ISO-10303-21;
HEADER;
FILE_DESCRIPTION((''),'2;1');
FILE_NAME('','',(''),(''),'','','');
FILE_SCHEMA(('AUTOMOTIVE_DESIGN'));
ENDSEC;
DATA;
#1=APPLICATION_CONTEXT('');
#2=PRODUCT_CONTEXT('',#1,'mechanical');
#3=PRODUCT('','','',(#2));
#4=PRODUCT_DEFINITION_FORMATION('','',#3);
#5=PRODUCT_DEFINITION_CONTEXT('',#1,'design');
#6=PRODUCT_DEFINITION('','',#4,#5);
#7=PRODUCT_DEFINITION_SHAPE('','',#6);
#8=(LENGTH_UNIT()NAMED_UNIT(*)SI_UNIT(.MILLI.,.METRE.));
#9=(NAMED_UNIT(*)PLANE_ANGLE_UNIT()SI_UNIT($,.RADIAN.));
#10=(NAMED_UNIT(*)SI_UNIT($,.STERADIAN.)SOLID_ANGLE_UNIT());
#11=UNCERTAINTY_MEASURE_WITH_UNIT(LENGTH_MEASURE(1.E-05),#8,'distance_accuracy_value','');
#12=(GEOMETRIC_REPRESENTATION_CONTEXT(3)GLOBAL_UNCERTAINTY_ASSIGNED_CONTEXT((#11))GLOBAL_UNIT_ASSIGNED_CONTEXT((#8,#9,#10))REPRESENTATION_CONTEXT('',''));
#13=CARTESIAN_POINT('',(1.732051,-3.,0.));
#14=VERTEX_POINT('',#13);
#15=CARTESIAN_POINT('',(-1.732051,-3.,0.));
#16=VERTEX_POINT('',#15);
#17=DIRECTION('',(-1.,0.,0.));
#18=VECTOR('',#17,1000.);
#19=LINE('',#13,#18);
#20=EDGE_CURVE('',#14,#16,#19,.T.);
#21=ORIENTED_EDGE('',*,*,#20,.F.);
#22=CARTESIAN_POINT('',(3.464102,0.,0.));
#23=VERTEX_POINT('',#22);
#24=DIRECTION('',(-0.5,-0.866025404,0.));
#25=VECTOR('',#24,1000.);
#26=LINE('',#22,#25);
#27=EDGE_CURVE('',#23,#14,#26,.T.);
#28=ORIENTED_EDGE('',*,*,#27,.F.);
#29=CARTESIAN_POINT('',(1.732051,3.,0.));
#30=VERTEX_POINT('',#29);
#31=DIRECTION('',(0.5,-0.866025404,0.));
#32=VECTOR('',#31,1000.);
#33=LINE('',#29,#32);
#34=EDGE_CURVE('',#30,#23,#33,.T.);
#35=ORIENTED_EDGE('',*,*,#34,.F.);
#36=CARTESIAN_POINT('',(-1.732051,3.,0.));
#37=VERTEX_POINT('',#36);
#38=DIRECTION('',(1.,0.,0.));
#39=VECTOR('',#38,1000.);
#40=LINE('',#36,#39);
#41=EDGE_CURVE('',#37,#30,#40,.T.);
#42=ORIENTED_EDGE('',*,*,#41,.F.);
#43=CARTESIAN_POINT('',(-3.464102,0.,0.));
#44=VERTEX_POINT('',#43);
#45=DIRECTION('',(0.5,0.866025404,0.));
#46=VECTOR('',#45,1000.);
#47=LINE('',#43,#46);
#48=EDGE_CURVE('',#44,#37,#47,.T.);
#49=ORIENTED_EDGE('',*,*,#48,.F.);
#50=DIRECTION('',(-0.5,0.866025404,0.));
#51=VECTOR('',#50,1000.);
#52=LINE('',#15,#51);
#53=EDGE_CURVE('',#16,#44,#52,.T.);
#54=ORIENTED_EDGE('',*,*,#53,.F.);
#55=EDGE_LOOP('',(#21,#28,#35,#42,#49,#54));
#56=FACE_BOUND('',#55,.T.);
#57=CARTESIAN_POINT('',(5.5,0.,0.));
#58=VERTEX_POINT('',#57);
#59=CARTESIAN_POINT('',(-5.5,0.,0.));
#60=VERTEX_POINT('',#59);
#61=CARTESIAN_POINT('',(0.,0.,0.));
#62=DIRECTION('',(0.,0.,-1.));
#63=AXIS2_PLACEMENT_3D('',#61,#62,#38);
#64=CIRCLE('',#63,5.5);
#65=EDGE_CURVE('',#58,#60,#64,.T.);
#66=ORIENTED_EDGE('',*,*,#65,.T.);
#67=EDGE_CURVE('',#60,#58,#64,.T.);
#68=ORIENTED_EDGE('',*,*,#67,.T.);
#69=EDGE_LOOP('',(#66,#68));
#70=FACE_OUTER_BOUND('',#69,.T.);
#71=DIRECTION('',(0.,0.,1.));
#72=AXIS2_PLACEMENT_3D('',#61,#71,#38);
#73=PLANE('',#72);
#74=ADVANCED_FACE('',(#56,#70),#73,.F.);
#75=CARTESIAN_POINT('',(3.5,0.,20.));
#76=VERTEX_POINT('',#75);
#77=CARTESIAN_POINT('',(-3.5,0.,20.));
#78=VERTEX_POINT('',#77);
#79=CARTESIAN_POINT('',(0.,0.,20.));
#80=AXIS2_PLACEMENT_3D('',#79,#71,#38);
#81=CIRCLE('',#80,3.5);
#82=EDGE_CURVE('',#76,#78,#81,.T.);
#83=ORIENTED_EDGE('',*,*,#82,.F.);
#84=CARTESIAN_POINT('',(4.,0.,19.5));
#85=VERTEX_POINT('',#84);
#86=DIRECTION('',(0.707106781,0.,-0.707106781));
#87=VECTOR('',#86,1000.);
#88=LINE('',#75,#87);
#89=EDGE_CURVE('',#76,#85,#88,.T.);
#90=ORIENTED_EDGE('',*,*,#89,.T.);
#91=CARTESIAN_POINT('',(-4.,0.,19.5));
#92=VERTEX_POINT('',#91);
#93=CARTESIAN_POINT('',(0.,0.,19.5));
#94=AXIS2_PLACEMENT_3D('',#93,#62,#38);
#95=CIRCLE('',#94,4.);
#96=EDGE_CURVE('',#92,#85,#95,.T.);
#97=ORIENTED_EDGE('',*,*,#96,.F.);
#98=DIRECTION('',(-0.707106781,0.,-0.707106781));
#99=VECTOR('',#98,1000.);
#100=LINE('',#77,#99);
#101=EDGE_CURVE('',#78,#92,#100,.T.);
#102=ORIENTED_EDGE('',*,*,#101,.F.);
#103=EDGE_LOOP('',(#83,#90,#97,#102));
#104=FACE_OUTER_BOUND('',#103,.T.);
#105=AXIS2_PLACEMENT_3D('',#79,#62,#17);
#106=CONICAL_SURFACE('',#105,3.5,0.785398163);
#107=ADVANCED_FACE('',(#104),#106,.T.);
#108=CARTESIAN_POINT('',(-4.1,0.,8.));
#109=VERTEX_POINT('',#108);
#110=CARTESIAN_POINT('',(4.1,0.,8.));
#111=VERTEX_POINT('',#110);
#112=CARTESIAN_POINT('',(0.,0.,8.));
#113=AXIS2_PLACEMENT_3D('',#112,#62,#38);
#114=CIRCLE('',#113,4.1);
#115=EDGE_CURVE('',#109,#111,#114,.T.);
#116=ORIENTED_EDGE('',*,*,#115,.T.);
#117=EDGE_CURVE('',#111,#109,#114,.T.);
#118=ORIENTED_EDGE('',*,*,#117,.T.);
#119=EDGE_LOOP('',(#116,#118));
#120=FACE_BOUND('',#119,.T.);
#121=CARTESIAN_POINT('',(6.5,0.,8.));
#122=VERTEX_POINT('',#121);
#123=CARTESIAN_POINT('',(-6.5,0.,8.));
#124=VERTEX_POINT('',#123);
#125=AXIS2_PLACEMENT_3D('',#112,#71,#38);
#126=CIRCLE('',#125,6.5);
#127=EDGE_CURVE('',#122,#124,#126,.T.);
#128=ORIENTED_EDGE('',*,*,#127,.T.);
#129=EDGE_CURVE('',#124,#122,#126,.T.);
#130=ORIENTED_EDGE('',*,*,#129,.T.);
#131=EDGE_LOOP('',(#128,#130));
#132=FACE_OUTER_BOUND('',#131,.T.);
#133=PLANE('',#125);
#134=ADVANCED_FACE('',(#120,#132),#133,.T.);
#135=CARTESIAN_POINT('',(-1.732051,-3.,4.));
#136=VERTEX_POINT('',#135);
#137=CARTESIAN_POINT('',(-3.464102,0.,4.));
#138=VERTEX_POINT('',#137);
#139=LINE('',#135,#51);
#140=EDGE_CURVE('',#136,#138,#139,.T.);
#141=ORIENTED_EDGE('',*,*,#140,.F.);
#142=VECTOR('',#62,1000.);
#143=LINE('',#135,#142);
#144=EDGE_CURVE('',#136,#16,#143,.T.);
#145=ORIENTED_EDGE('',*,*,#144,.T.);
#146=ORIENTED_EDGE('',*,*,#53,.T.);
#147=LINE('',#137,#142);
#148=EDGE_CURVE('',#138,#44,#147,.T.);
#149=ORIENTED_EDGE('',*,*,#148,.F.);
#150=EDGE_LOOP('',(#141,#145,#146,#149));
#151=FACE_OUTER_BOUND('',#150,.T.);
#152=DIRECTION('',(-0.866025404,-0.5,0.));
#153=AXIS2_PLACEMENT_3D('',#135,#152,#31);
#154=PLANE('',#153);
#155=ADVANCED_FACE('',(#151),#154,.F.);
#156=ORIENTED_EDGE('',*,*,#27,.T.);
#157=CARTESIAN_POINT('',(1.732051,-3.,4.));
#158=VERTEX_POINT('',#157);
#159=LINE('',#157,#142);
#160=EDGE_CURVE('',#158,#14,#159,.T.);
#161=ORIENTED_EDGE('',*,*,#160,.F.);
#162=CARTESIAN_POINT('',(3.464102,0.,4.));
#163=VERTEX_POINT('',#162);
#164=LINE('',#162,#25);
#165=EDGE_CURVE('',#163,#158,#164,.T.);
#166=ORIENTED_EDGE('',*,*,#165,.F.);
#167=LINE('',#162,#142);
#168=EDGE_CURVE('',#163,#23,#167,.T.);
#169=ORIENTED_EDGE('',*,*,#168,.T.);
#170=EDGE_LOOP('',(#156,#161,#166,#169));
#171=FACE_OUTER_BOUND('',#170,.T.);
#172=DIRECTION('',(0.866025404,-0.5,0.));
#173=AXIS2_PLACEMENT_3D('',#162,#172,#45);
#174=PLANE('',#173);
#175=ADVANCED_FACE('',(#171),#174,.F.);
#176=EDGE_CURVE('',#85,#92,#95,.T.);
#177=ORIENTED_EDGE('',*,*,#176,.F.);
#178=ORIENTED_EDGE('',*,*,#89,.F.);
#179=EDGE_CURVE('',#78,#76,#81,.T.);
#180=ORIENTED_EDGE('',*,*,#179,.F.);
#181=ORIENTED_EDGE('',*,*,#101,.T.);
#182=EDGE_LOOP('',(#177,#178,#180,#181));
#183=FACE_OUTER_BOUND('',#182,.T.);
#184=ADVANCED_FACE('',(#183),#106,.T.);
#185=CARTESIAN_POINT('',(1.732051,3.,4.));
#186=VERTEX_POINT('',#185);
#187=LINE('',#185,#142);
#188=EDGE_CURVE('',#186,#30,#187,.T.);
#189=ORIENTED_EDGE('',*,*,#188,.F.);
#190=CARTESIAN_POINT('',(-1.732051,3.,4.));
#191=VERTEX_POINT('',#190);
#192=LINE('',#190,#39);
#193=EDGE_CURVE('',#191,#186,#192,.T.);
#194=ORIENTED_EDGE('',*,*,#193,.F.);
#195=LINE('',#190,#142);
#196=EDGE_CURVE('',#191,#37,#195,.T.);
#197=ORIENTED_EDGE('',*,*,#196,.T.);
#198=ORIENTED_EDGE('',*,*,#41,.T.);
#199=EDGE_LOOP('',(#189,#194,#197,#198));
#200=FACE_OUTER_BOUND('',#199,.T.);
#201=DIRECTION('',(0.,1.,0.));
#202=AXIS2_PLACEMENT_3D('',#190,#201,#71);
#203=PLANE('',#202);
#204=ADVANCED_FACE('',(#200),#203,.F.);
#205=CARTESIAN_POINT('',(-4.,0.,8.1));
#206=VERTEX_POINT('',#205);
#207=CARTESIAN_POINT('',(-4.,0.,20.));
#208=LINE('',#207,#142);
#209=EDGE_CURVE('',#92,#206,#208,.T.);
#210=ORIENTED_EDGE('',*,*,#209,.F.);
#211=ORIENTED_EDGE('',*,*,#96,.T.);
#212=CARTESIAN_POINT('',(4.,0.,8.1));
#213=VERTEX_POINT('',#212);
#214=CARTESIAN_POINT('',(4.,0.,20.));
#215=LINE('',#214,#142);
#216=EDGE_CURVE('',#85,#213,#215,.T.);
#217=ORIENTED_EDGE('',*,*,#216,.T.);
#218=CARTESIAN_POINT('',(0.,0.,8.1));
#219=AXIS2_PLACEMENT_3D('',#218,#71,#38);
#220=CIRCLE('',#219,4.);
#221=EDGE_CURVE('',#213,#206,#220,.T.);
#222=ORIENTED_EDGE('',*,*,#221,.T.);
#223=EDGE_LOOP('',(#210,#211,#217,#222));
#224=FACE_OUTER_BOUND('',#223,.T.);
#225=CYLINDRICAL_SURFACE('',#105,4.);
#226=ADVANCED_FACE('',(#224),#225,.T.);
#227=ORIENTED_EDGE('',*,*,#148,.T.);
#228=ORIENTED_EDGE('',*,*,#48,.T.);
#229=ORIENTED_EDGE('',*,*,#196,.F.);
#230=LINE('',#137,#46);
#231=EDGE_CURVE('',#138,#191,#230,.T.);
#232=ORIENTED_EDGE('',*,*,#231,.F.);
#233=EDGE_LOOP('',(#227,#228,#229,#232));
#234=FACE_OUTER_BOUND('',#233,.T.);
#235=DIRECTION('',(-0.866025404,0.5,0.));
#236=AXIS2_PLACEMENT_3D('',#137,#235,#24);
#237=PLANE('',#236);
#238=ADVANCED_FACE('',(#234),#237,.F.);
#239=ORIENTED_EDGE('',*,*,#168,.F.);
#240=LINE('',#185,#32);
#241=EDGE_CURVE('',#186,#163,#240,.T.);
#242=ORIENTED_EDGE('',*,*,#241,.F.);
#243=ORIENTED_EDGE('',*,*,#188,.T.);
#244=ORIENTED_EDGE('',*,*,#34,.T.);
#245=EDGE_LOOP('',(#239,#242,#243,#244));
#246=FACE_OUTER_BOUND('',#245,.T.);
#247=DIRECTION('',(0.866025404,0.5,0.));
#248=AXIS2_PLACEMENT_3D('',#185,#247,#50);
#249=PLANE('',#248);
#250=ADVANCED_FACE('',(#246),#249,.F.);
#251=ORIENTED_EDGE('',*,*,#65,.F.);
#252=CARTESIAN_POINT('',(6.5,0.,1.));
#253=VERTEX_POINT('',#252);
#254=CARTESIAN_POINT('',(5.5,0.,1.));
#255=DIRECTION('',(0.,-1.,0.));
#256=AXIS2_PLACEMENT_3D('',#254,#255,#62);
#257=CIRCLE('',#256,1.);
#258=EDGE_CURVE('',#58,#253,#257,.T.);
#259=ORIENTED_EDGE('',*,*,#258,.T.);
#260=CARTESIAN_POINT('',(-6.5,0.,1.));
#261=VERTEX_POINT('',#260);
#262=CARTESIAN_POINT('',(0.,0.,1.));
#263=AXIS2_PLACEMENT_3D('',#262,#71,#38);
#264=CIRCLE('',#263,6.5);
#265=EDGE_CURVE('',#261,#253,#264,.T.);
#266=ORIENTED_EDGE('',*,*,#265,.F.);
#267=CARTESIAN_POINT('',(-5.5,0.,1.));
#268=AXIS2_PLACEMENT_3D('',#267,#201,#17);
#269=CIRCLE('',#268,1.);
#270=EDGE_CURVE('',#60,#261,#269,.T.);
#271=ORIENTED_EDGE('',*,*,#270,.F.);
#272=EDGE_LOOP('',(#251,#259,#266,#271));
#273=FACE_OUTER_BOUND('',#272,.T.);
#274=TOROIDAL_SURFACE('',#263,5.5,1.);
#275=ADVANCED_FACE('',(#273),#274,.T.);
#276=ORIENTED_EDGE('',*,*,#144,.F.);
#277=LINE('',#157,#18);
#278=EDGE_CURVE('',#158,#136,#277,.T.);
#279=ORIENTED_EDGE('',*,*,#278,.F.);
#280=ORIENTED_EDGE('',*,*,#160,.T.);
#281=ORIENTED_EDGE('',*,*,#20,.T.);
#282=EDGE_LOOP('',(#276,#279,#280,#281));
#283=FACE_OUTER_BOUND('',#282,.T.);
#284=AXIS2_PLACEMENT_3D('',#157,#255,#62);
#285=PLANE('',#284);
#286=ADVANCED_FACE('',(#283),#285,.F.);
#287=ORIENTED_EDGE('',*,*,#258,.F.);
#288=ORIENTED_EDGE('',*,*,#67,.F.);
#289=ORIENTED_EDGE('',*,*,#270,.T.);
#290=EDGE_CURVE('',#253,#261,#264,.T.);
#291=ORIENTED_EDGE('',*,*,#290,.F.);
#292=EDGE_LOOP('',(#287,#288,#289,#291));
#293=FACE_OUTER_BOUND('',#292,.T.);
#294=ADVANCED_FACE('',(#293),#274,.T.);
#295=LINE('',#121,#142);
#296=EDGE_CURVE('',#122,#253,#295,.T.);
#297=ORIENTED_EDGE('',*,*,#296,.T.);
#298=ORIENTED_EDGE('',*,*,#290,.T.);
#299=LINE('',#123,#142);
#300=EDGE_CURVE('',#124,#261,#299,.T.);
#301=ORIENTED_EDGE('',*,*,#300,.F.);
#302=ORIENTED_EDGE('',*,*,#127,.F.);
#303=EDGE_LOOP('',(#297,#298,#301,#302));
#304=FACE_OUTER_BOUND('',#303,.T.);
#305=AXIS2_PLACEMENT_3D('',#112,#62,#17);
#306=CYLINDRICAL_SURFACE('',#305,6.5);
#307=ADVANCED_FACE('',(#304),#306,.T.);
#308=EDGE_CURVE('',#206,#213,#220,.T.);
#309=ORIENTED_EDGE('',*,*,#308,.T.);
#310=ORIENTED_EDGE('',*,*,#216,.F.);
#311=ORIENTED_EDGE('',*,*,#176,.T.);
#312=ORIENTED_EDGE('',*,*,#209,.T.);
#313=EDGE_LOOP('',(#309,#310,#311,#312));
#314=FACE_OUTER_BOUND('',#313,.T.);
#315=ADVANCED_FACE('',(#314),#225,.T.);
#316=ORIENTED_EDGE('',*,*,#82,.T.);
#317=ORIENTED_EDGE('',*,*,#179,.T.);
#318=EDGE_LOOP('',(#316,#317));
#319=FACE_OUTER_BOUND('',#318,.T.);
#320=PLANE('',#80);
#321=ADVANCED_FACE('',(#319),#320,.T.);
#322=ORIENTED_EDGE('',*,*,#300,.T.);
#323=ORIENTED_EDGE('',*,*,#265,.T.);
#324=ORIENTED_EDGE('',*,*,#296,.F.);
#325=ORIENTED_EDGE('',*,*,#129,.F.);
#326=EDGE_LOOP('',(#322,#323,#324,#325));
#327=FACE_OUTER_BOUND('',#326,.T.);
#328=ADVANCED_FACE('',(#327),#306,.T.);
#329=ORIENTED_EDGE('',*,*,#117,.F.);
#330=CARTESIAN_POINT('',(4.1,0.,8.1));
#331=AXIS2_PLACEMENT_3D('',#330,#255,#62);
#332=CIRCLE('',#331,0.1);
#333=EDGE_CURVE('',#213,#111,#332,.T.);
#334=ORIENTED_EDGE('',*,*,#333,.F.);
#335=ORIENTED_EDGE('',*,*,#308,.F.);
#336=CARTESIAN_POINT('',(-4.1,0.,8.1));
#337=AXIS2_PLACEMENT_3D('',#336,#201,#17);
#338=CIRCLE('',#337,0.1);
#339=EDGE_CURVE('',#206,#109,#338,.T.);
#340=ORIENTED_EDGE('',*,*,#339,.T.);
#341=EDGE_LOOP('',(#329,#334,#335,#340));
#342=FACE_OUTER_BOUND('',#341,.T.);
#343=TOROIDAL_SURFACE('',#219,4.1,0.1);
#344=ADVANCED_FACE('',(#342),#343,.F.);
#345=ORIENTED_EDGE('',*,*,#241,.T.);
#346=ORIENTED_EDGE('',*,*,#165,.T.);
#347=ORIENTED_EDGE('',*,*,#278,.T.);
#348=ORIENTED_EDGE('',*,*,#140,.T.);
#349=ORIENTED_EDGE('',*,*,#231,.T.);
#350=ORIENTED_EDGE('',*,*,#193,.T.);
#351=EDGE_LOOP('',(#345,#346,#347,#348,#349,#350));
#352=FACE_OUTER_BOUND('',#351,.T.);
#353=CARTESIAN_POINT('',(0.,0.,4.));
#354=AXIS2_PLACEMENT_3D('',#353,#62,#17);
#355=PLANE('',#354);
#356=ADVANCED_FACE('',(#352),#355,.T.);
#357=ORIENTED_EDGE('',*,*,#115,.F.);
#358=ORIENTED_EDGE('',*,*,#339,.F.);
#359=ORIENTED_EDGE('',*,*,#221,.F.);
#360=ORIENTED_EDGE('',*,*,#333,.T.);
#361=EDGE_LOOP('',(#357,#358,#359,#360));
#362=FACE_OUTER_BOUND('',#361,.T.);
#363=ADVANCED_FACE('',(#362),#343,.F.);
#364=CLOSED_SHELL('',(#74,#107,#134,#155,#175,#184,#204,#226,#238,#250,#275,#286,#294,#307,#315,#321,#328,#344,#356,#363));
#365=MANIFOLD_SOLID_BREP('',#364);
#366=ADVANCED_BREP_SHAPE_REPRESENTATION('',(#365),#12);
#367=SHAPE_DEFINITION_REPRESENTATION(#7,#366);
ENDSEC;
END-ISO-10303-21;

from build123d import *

# Parameters (mm, degrees)
SKETCH_1_R          = 6.5
EXTRUDE_1_DEPTH     = 8
SKETCH_2_R          = 4
EXTRUDE_2_DEPTH     = 12
CUT_EXTRUDE_1_DEPTH = 4
FILLET_1_R          = 0.1
CHAMFER_1_SIZE      = 0.5
FILLET_2_R          = 1


with BuildPart() as part:
    # 草图1 → 凸台-拉伸1 (new body)
    with BuildSketch(Plane.XY):
        Circle(SKETCH_1_R)
    extrude(amount=EXTRUDE_1_DEPTH)

    # 草图2 → 凸台-拉伸2 (add)
    with BuildSketch(Plane.XY.offset(8)):
        Circle(SKETCH_2_R)
    extrude(amount=EXTRUDE_2_DEPTH)

    # 草图3 → 切除-拉伸1 (cut)
    with BuildSketch(Plane(origin=(0, 0, 0), x_dir=(-1, 0, 0), z_dir=(0, 0, -1))):
        Polygon((1.732050808, -3), (3.464101615, 0), (1.732050808, 3), (-1.732050808, 3), (-3.464101615, 0), (-1.732050808, -3), align=None)
    extrude(amount=-CUT_EXTRUDE_1_DEPTH, mode=Mode.SUBTRACT)

    # 圆角1
    fillet_1_edges = [part.edges().sort_by_distance(p)[0] for p in [
        (-4, 0, 8),
    ]]
    fillet(fillet_1_edges, radius=FILLET_1_R)

    # 倒角1
    chamfer_1_edges = [part.edges().sort_by_distance(p)[0] for p in [
        (-4, 0, 20),
    ]]
    chamfer(chamfer_1_edges, length=CHAMFER_1_SIZE)

    # 圆角2
    fillet_2_edges = [part.edges().sort_by_distance(p)[0] for p in [
        (-6.5, 0, 0),
    ]]
    fillet(fillet_2_edges, radius=FILLET_2_R)


solid = part.part
